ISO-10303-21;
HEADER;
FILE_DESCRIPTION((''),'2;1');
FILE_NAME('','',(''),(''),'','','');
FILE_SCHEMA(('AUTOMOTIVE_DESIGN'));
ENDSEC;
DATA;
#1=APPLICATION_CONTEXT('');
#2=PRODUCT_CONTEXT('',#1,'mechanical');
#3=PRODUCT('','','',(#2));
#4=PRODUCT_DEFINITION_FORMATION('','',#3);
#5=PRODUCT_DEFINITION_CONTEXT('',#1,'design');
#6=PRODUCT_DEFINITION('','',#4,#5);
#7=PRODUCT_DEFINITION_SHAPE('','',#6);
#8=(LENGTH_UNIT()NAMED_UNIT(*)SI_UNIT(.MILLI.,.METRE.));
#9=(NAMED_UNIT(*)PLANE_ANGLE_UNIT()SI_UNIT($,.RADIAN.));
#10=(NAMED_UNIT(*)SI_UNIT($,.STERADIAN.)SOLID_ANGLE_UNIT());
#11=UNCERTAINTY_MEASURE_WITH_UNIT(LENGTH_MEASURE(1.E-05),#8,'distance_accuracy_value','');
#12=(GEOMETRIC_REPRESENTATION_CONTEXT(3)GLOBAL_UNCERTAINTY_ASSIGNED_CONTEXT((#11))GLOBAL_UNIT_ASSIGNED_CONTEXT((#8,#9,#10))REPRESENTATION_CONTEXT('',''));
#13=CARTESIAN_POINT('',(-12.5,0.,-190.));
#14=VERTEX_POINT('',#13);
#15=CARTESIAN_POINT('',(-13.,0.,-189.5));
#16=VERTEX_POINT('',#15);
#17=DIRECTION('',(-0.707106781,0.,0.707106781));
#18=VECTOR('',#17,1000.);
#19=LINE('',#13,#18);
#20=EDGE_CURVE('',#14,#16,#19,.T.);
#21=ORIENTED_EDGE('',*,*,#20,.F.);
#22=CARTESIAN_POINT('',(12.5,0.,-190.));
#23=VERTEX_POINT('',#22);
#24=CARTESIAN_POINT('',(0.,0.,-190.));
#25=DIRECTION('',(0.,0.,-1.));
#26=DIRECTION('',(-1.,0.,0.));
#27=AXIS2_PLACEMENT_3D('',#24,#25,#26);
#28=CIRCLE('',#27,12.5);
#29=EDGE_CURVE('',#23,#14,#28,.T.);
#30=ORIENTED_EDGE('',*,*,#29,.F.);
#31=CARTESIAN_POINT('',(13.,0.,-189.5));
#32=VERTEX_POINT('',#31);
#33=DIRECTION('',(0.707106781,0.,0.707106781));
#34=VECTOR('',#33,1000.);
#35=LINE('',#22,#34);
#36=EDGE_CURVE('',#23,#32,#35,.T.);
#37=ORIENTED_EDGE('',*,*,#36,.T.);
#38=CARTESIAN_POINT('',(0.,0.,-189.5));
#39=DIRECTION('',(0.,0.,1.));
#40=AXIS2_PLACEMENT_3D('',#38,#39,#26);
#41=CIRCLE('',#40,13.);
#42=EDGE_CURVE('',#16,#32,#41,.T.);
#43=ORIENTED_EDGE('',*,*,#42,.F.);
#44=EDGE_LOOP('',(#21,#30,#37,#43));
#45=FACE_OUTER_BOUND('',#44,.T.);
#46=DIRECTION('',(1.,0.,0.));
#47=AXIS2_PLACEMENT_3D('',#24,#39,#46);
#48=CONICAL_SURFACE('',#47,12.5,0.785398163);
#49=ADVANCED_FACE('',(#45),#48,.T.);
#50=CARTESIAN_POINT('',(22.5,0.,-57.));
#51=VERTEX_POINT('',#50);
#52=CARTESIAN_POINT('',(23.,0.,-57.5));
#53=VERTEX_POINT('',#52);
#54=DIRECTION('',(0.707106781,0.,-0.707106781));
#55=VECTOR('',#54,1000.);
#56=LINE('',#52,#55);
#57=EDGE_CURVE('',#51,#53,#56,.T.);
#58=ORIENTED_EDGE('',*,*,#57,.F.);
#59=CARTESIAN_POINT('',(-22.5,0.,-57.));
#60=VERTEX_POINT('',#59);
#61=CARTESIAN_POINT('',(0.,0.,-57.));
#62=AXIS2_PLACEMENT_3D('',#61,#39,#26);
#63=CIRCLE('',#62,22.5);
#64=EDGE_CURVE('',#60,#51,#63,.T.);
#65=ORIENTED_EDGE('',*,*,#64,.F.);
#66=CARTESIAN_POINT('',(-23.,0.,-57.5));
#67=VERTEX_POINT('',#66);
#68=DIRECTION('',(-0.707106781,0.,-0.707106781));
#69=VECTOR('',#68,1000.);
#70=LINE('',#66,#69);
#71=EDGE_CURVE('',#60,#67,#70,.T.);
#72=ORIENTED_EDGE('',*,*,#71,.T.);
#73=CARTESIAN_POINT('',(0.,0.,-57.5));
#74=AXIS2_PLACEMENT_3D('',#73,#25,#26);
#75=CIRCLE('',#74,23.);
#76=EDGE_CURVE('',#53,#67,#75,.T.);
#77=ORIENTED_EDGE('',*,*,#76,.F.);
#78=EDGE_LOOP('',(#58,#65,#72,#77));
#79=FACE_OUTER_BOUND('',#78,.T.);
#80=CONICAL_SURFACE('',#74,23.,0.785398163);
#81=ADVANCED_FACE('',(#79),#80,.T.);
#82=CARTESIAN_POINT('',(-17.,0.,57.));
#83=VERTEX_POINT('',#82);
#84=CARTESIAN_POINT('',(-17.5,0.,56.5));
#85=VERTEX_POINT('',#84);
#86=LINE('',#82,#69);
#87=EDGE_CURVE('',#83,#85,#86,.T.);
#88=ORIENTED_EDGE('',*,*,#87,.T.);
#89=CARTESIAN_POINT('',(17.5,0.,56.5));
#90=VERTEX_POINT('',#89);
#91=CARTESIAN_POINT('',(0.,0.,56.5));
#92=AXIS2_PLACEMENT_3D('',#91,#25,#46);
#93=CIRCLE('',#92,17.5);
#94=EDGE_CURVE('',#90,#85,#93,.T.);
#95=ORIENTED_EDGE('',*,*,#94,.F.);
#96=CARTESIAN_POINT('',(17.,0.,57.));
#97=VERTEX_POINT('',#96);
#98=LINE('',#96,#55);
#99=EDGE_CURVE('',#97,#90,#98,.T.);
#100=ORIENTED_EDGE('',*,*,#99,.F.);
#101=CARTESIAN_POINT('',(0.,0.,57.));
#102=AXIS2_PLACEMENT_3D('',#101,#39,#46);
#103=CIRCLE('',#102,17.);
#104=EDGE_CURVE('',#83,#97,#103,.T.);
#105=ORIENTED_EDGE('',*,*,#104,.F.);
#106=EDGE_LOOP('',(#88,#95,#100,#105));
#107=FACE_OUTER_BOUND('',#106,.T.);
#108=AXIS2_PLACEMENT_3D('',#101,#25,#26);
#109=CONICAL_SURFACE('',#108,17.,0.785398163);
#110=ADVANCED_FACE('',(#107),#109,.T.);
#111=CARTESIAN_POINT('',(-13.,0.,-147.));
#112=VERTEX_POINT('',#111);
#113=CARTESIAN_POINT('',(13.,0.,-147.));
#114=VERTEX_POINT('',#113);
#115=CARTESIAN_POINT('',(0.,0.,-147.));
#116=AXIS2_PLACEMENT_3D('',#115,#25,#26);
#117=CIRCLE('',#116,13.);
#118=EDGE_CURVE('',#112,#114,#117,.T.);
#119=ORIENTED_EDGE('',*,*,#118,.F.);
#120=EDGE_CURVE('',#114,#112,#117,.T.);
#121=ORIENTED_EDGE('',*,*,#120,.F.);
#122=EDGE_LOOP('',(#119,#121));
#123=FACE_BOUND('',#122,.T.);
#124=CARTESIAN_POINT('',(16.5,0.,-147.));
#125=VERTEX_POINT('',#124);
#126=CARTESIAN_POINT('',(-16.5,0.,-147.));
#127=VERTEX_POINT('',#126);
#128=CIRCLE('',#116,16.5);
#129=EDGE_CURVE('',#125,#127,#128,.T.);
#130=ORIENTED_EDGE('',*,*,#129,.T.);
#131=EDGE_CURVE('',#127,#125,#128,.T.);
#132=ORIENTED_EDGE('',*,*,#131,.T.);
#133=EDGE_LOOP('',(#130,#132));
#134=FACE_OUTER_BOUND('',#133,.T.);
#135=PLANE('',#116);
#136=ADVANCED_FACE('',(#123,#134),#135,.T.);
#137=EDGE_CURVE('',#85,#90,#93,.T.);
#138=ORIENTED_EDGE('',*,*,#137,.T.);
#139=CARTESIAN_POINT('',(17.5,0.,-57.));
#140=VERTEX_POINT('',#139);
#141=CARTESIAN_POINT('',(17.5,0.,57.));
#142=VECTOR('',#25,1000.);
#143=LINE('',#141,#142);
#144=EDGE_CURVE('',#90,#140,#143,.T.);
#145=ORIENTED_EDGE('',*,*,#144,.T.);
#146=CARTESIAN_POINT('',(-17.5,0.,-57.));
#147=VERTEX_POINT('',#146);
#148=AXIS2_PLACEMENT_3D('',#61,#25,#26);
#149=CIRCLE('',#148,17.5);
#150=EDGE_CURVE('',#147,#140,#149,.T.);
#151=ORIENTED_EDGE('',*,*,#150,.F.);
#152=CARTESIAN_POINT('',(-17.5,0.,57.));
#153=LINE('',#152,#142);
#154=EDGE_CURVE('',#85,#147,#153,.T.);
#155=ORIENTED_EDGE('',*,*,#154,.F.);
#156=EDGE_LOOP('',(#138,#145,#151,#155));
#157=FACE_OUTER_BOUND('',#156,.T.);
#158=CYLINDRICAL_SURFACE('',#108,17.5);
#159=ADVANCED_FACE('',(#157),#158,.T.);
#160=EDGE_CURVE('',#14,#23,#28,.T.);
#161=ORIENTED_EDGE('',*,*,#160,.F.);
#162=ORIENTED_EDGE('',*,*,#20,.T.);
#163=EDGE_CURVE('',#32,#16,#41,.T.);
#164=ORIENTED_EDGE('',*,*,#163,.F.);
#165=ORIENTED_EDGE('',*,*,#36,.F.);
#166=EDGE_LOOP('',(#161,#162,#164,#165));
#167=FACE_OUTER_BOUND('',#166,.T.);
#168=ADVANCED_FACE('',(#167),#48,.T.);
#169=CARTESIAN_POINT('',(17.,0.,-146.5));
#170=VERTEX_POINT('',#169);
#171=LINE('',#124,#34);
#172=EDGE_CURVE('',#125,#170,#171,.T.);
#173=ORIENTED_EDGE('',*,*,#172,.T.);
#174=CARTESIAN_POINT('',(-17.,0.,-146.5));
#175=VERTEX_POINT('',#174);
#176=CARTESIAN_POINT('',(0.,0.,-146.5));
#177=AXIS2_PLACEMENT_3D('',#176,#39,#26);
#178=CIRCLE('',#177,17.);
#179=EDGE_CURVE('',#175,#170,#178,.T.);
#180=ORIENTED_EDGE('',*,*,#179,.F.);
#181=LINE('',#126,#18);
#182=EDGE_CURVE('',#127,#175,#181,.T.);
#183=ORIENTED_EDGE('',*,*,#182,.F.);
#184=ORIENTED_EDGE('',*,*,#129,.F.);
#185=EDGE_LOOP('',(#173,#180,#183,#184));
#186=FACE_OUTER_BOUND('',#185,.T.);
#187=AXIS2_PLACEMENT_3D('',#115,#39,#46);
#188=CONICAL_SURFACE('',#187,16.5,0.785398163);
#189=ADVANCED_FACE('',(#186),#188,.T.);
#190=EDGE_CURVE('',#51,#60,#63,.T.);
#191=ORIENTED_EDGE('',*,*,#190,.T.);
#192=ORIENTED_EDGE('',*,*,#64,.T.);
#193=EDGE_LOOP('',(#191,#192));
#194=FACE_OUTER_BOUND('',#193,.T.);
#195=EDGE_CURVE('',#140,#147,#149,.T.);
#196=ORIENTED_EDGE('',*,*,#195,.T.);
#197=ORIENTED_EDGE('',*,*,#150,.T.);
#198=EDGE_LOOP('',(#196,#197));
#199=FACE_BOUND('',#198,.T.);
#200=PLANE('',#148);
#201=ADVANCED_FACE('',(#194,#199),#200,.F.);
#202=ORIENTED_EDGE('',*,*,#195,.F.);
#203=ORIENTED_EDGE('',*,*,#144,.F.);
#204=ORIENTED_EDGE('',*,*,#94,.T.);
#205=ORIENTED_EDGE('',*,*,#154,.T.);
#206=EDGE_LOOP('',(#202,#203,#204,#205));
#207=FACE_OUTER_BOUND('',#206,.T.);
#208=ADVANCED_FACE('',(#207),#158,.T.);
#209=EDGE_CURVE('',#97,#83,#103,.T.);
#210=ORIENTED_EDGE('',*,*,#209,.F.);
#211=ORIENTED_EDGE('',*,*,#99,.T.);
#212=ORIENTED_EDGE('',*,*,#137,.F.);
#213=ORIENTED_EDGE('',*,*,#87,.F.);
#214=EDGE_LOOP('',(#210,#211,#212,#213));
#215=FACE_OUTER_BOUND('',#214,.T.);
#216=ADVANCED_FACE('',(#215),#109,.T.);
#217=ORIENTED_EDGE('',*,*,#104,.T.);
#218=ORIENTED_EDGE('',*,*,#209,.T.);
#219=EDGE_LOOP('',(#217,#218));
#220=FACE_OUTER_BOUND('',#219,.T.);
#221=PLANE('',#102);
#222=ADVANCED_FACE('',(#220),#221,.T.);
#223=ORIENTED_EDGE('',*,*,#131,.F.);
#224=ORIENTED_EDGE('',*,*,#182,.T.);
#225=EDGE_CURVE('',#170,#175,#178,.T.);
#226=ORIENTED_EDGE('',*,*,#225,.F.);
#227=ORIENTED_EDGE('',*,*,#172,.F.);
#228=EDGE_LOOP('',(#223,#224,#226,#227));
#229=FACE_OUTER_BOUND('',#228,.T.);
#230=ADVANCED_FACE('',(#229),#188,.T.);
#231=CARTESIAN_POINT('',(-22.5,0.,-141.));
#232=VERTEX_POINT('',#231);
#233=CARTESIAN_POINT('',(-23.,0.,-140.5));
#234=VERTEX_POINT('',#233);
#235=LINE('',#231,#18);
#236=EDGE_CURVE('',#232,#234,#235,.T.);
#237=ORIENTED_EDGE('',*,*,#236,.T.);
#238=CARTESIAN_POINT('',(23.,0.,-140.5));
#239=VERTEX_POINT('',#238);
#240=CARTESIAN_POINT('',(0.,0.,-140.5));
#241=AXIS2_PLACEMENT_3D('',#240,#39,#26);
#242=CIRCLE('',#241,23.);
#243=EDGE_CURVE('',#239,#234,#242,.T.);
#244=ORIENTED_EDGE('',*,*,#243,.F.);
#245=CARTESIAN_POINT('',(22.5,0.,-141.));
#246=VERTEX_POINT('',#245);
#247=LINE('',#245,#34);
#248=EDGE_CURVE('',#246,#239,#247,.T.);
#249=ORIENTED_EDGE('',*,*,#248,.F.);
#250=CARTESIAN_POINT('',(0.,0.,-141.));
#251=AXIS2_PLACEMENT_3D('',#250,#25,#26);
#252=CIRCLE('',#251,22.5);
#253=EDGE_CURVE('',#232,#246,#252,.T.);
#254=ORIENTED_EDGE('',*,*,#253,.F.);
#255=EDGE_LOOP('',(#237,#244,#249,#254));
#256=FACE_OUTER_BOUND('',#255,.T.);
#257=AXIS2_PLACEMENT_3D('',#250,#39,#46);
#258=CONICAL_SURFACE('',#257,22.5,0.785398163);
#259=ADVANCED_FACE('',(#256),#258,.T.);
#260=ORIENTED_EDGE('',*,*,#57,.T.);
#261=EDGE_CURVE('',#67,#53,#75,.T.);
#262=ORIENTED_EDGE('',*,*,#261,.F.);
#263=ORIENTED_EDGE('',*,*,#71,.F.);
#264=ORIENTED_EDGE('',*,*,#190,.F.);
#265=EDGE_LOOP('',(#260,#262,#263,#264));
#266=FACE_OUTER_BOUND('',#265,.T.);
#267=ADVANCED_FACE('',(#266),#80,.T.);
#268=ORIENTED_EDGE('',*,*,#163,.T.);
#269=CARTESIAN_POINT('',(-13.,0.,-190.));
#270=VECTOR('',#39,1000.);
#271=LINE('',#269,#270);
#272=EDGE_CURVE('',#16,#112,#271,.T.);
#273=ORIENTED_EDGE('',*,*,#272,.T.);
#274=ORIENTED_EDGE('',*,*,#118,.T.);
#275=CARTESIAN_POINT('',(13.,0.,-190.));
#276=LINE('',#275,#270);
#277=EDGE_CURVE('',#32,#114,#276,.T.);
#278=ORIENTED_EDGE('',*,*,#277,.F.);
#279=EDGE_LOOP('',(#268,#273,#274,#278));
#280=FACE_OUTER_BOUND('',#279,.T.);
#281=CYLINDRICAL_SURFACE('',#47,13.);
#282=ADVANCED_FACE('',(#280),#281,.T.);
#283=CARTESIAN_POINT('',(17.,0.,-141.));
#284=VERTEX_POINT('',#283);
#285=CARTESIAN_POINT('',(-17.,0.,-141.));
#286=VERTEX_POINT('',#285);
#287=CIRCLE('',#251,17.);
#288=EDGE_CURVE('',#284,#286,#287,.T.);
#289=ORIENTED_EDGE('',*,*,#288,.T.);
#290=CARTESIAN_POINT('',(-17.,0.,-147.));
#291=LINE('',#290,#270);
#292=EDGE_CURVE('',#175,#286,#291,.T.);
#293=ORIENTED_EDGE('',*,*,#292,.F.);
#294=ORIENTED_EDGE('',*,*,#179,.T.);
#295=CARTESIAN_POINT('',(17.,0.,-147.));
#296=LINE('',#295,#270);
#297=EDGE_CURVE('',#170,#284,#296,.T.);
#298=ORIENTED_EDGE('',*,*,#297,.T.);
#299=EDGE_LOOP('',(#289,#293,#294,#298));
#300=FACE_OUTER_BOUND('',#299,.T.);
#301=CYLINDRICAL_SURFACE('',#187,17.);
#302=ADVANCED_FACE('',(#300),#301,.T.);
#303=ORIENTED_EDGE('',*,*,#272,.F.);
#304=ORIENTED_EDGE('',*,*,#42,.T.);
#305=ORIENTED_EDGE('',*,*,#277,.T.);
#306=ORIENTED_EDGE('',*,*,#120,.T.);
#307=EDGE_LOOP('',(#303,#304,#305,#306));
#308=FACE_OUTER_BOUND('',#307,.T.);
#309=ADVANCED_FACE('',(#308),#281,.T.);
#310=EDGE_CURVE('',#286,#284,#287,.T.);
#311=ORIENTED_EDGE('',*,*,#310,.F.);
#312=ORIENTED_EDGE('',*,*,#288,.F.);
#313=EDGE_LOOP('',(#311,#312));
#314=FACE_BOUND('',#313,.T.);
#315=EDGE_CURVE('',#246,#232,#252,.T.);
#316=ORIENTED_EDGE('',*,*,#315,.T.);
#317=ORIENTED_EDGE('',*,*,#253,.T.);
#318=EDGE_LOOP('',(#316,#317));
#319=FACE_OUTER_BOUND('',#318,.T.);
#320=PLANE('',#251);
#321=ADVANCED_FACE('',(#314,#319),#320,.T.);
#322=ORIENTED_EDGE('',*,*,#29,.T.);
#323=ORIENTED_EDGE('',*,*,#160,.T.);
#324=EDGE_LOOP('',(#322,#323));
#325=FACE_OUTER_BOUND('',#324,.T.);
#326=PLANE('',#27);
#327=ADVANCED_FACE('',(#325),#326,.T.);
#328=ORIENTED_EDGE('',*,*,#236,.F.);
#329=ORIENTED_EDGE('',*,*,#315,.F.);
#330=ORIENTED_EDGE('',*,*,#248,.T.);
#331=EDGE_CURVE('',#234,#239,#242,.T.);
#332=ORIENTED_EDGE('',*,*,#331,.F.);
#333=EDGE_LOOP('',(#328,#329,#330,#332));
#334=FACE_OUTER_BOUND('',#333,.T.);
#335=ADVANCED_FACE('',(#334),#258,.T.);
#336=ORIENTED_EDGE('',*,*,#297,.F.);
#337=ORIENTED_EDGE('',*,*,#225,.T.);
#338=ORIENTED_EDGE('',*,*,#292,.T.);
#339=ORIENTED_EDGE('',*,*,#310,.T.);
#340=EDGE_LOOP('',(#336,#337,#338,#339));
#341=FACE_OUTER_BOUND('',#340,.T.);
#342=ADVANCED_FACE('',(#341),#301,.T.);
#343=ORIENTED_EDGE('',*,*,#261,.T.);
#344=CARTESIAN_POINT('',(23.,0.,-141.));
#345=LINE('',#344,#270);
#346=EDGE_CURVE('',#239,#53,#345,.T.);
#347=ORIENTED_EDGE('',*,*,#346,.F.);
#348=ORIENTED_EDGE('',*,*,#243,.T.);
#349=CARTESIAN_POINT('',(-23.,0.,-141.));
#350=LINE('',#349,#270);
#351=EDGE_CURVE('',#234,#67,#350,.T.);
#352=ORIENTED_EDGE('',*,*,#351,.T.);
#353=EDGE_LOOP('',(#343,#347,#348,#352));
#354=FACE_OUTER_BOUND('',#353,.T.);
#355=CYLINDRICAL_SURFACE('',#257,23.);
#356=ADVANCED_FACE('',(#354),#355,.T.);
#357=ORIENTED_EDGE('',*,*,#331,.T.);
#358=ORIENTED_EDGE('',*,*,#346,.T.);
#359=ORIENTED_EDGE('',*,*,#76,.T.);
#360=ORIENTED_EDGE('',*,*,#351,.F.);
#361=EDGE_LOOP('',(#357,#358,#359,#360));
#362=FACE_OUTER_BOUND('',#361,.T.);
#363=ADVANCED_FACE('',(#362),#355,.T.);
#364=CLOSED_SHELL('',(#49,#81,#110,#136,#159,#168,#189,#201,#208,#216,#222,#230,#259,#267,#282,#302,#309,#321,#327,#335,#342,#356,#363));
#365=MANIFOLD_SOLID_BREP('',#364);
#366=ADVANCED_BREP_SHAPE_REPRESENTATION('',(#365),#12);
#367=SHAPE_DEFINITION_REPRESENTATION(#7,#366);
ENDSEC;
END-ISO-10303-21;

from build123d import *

# Parameters (mm, degrees)
SKETCH_1_R      = 17.5
EXTRUDE_1_DEPTH = 57
SKETCH_2_R      = 23
EXTRUDE_2_DEPTH = 84
SKETCH_3_R      = 17
EXTRUDE_3_DEPTH = 6
SKETCH_4_R      = 13
EXTRUDE_4_DEPTH = 43
CHAMFER_1_SIZE  = 0.5


with BuildPart() as part:
    # 草图1 → 凸台-拉伸1 (new, symmetric)
    with BuildSketch(Plane.XY):
        with Locations(Location((0, 0, 0), (0, 0, 180))):
            Circle(SKETCH_1_R)
    extrude(amount=EXTRUDE_1_DEPTH, both=True)

    # 草图2 → 凸台-拉伸2 (add)
    with BuildSketch(Plane(origin=(0, 0, -57), x_dir=(-1, 0, 0), z_dir=(0, 0, -1))):
        with Locations(Location((0, 0, 0), (0, 0, 180))):
            Circle(SKETCH_2_R)
    extrude(amount=EXTRUDE_2_DEPTH)

    # 草图3 → 凸台-拉伸3 (add)
    with BuildSketch(Plane(origin=(0, 0, -141), x_dir=(-1, 0, 0), z_dir=(0, 0, -1))):
        Circle(SKETCH_3_R)
    extrude(amount=EXTRUDE_3_DEPTH)

    # 草图4 → 凸台-拉伸4 (add)
    with BuildSketch(Plane(origin=(0, 0, -147), x_dir=(-1, 0, 0), z_dir=(0, 0, -1))):
        Circle(SKETCH_4_R)
    extrude(amount=EXTRUDE_4_DEPTH)

    # 倒角1
    chamfer_1_edges = [part.edges().sort_by_distance(p)[0] for p in [
        (17, 0, -147),
        (13, 0, -190),
        (17.5, 0, 57),
        (-23, 0, -57),
        (-23, 0, -141),
    ]]
    chamfer(chamfer_1_edges, length=CHAMFER_1_SIZE)


solid = part.part
